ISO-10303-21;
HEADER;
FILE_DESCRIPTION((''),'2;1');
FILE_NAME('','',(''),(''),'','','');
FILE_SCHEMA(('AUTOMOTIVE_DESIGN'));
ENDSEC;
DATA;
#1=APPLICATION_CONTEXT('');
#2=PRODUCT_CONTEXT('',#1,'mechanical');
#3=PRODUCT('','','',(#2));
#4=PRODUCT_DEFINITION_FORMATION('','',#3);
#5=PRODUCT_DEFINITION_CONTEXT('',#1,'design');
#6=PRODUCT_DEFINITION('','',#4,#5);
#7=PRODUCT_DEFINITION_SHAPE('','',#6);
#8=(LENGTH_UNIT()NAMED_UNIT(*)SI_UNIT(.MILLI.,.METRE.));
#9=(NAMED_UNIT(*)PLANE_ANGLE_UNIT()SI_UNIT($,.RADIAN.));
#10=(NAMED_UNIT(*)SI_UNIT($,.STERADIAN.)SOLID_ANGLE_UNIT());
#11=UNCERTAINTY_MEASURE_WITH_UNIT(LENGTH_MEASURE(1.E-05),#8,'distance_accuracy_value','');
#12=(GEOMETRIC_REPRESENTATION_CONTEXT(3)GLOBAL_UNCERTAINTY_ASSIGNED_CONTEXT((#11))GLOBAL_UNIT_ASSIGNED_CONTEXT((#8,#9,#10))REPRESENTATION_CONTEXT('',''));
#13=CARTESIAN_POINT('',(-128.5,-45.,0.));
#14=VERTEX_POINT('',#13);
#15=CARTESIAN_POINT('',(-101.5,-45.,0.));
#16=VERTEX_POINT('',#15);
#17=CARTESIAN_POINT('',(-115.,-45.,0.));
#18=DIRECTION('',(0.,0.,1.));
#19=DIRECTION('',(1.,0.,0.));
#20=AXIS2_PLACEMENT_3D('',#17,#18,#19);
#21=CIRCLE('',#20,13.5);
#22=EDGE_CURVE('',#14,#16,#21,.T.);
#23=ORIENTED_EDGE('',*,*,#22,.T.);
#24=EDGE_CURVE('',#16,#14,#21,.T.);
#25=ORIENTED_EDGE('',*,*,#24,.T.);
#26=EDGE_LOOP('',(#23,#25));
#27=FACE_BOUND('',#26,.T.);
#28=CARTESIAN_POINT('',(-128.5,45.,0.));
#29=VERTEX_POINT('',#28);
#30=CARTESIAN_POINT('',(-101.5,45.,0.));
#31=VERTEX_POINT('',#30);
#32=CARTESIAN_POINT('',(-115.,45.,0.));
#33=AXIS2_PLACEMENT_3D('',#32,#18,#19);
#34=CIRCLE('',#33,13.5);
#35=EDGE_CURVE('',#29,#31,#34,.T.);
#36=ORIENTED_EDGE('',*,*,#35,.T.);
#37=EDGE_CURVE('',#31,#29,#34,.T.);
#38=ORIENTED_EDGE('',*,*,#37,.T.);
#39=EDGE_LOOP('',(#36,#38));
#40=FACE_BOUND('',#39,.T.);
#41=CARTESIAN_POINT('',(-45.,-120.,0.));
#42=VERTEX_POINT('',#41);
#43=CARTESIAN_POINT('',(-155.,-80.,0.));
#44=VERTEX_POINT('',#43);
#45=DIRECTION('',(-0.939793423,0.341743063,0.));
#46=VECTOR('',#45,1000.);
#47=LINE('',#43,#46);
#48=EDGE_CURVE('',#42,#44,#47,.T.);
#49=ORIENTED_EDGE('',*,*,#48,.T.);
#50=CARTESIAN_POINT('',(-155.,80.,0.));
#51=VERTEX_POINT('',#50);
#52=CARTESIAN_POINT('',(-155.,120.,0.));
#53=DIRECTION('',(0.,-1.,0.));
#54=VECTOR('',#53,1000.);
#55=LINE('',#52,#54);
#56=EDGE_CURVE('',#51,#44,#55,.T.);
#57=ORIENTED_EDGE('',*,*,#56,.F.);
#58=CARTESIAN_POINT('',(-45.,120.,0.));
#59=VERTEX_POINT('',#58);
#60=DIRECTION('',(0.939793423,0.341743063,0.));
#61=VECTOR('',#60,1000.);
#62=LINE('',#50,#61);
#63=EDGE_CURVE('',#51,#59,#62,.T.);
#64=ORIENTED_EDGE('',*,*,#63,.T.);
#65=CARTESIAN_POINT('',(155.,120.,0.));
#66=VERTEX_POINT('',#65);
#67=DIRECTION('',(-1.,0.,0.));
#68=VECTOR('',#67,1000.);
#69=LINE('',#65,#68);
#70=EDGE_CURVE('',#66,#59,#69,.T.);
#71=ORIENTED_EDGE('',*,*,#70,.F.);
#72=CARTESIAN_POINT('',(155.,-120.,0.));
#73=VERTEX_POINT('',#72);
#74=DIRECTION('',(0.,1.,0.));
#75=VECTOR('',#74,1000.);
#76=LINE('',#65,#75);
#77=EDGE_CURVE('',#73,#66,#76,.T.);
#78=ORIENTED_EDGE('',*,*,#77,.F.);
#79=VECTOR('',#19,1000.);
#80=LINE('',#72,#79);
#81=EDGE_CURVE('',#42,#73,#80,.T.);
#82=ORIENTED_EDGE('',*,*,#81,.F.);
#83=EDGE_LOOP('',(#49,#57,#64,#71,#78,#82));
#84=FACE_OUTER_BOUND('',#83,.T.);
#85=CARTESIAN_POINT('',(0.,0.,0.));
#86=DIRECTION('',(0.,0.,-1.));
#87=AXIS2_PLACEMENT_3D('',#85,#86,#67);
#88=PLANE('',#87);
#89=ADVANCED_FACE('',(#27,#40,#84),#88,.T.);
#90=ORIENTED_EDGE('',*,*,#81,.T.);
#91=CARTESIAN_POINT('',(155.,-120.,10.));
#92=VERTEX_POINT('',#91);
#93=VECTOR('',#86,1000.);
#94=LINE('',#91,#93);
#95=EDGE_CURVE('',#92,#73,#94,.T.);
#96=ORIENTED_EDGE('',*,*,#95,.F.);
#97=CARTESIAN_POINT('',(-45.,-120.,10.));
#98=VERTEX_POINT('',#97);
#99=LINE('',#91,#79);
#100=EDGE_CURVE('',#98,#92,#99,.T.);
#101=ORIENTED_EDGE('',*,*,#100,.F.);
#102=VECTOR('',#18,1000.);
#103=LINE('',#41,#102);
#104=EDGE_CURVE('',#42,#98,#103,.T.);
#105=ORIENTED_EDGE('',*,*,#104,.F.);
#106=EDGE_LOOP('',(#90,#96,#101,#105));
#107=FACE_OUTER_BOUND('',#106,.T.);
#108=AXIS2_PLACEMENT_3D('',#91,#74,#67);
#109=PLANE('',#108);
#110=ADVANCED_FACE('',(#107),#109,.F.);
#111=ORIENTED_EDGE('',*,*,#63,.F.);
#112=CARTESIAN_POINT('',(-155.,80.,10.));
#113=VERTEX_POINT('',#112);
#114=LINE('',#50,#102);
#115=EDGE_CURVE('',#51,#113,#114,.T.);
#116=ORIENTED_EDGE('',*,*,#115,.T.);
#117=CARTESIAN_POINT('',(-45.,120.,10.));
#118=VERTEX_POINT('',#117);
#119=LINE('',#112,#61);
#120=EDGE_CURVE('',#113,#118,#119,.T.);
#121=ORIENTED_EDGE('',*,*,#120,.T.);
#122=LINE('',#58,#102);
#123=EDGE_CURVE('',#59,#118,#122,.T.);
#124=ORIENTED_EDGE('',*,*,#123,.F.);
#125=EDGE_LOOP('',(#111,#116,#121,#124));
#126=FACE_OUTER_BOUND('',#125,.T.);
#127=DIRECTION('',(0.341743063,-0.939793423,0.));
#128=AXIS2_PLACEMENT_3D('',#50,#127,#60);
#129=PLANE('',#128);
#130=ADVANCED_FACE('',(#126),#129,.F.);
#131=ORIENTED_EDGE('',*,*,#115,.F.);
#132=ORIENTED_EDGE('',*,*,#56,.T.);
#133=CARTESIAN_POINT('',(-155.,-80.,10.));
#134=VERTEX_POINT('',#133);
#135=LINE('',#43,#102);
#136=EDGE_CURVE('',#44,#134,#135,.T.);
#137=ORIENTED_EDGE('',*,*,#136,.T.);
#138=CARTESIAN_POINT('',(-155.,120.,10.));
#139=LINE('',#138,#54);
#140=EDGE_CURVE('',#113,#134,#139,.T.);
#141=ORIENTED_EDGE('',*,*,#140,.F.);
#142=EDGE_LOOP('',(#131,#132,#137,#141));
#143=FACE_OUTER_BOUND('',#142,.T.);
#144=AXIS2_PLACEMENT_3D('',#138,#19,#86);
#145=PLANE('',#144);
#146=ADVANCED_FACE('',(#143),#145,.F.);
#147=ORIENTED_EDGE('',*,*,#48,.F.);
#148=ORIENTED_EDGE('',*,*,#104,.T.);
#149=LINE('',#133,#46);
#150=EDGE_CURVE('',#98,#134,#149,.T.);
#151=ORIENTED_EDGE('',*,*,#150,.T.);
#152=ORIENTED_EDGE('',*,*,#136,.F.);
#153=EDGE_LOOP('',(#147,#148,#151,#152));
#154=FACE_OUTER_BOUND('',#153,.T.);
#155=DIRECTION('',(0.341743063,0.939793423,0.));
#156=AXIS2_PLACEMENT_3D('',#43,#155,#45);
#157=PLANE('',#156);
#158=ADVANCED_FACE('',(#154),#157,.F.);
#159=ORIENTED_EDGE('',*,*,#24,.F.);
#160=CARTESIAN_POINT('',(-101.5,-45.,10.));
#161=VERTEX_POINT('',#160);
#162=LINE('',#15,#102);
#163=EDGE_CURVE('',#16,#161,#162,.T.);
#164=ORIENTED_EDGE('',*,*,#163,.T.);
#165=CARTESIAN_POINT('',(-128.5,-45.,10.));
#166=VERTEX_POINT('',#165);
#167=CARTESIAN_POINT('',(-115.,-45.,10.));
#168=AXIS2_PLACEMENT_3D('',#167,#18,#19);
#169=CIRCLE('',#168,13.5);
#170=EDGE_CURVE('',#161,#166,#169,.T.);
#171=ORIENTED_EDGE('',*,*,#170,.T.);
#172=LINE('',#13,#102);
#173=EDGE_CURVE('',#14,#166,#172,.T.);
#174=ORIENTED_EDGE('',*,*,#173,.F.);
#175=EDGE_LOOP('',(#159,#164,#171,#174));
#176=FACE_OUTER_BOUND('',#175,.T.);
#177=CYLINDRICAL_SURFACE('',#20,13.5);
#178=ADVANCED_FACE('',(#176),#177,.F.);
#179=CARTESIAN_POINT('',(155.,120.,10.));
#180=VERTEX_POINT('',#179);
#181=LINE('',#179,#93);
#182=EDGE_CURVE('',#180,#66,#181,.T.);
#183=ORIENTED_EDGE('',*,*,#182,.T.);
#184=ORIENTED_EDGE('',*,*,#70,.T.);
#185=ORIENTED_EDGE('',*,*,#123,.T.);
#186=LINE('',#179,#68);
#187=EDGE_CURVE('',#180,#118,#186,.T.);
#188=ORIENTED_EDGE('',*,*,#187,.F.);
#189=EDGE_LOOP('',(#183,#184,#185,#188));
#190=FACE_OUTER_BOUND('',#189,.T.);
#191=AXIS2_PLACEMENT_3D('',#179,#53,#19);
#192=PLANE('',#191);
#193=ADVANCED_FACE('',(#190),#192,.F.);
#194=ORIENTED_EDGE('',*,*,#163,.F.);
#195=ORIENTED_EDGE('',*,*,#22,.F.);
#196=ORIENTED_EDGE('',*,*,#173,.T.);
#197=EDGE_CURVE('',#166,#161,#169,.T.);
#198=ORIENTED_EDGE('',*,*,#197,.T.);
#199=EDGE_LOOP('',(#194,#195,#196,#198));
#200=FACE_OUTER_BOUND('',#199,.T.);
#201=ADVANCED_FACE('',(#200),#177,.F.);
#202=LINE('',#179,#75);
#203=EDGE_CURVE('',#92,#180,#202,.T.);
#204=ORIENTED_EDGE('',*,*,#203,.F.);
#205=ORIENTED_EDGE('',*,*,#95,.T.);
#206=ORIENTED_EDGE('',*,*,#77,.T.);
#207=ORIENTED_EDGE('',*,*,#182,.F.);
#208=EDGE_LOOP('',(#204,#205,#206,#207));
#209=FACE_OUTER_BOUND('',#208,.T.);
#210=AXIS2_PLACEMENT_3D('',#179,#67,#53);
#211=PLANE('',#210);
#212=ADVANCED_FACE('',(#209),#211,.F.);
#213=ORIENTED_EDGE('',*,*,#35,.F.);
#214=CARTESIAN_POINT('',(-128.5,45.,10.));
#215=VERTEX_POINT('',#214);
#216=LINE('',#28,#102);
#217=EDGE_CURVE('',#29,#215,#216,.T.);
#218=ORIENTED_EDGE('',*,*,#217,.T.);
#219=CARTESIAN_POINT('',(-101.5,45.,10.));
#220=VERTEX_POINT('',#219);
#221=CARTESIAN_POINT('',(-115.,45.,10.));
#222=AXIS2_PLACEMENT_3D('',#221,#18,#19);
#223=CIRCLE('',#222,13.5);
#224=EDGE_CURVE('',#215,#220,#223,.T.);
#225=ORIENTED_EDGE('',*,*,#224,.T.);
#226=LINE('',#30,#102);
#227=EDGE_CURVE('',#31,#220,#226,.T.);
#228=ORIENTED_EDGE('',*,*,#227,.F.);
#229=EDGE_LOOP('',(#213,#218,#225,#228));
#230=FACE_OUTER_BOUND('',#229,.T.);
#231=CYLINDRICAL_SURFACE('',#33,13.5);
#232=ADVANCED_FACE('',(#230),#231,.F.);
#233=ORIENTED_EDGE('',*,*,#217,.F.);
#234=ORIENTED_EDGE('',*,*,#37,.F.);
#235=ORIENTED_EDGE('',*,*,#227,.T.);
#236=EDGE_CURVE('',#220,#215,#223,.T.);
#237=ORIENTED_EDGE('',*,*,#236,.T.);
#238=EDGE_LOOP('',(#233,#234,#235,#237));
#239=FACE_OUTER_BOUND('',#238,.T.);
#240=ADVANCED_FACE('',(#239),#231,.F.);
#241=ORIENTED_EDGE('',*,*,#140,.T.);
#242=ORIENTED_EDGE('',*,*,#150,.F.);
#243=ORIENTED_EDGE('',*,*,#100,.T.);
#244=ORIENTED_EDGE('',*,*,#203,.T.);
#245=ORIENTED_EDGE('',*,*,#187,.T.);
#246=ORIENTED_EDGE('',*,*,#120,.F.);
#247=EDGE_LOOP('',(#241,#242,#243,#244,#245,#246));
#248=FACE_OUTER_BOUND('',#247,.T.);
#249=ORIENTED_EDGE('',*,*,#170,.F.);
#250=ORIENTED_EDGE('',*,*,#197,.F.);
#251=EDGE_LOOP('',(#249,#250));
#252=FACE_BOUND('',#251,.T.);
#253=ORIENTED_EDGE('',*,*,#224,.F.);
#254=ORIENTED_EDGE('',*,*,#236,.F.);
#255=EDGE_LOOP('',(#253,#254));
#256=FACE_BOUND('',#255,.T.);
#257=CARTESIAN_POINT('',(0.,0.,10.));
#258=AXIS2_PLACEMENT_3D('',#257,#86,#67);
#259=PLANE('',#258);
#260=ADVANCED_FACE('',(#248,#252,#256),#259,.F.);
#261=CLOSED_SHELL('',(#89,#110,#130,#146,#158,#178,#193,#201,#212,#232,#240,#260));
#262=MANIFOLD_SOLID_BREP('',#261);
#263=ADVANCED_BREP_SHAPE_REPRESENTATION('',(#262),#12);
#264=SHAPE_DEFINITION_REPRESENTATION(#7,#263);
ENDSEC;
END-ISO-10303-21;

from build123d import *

# Parameters (mm, degrees)
SKETCH_1_W          = 310
SKETCH_1_H          = 240
EXTRUDE_1_DEPTH     = 10
SKETCH_2_R          = 13.5
CUT_EXTRUDE_1_DEPTH = 10


with BuildPart() as part:
    # 草图1 → 凸台-拉伸1 (new body)
    with BuildSketch(Plane.XY):
        Rectangle(SKETCH_1_W, SKETCH_1_H)
    extrude(amount=EXTRUDE_1_DEPTH)

    # 草图2 → 切除-拉伸1 (cut)
    with BuildSketch(Plane.XY.offset(10)):
        with Locations((-115, -45)):
            Circle(SKETCH_2_R)
        with Locations((-115, 45)):
            Circle(SKETCH_2_R)
        Polygon((-155, -80), (-45, -120), (-155, -120), align=None)
        Polygon((-155, 80), (-45, 120), (-155, 120), align=None)
    extrude(amount=-CUT_EXTRUDE_1_DEPTH, mode=Mode.SUBTRACT)


solid = part.part
